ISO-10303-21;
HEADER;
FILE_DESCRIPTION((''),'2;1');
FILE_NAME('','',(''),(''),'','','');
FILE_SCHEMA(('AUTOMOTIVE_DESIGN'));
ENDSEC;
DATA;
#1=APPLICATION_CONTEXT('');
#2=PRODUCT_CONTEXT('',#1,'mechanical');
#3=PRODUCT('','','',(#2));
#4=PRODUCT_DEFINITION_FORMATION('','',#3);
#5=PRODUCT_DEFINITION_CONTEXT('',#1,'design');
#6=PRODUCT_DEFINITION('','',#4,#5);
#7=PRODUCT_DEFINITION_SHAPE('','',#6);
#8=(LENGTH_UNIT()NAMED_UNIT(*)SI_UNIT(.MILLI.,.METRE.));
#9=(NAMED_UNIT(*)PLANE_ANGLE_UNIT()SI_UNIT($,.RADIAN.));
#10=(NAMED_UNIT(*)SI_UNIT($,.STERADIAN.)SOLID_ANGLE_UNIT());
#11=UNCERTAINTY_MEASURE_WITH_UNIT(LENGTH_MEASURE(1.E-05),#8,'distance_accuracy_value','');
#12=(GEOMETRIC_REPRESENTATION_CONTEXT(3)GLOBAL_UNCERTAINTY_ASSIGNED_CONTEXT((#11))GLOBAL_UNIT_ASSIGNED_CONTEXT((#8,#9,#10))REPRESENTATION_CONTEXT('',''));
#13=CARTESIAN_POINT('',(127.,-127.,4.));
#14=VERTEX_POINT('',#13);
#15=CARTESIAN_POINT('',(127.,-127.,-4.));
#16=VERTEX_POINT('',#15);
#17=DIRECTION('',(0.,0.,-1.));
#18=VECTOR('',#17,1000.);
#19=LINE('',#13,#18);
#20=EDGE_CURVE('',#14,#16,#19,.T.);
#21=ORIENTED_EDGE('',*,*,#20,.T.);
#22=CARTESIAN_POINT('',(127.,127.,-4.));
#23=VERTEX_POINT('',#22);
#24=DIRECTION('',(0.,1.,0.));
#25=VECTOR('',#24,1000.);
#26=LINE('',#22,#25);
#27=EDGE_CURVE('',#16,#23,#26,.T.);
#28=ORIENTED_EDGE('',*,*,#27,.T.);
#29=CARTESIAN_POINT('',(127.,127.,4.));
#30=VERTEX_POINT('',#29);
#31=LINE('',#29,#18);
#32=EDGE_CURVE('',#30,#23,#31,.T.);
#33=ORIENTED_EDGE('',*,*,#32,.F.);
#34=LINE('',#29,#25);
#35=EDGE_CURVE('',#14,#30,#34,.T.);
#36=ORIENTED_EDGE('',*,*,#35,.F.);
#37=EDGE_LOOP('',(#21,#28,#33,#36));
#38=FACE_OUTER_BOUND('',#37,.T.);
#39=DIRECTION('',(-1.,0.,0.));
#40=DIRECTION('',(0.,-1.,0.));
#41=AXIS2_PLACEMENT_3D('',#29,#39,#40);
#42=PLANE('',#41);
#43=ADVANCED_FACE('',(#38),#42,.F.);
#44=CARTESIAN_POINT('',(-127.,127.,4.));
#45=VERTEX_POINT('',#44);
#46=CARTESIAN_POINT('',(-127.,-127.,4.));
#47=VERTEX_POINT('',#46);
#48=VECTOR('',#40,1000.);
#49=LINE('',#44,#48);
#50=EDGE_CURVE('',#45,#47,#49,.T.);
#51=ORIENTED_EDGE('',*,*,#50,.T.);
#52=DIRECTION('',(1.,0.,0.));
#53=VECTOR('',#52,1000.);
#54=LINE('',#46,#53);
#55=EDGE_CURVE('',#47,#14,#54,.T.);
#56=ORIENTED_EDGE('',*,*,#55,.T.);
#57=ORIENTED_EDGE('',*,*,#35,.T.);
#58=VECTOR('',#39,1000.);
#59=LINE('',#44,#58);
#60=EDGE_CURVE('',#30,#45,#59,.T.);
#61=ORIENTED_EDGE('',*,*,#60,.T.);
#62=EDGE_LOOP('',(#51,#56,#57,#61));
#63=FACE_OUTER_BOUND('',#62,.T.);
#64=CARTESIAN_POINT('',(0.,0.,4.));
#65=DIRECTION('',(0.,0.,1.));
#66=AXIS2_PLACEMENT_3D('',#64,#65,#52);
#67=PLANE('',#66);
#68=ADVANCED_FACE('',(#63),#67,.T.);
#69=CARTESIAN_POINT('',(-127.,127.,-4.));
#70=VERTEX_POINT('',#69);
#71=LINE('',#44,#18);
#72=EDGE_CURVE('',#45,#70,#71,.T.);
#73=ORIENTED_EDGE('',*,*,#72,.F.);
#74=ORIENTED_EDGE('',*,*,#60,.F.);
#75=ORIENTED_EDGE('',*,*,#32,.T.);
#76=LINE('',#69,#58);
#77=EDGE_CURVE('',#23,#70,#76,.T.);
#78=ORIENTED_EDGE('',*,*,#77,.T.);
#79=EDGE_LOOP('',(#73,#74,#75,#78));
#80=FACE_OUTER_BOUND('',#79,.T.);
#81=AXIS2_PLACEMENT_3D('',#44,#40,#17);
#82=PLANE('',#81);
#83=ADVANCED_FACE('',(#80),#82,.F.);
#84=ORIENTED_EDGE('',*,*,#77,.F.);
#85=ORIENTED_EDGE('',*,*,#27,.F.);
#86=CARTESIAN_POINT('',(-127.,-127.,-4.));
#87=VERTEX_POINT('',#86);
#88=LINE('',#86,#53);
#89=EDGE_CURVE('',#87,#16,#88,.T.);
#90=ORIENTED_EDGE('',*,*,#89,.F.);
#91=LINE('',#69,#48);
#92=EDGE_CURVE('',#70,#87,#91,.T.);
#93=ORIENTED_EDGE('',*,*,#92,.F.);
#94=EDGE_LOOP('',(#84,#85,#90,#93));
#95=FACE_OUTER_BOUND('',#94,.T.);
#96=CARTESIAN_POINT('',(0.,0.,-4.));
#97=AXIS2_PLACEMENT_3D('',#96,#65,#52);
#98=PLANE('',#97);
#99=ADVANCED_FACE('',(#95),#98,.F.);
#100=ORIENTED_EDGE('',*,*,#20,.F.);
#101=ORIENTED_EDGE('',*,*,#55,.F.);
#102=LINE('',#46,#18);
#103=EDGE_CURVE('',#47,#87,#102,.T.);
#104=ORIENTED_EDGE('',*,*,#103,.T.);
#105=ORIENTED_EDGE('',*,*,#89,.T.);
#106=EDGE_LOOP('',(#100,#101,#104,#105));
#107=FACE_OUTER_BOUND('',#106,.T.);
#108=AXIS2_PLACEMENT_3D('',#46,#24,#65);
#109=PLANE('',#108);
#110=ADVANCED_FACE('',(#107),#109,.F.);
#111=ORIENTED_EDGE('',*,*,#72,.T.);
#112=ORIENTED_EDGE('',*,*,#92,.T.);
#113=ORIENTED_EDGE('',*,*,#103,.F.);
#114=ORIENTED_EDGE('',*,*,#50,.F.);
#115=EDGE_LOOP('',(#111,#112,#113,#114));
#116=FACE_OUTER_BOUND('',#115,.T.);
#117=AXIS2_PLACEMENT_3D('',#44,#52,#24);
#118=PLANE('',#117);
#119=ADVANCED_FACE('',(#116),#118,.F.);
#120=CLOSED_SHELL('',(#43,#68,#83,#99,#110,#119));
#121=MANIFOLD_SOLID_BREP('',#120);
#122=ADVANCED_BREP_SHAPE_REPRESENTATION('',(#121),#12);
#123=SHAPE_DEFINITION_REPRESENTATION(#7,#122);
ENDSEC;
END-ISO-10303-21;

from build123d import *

# Parameters (mm, degrees)
SKETCH1_W           = 254
SKETCH1_H           = 254
BOSS_EXTRUDE1_DEPTH = 4


with BuildPart() as part:
    # Sketch1 → Boss-Extrude1 (new, symmetric)
    with BuildSketch(Plane.XY):
        Rectangle(SKETCH1_W, SKETCH1_H)
    extrude(amount=BOSS_EXTRUDE1_DEPTH, both=True)


solid = part.part
